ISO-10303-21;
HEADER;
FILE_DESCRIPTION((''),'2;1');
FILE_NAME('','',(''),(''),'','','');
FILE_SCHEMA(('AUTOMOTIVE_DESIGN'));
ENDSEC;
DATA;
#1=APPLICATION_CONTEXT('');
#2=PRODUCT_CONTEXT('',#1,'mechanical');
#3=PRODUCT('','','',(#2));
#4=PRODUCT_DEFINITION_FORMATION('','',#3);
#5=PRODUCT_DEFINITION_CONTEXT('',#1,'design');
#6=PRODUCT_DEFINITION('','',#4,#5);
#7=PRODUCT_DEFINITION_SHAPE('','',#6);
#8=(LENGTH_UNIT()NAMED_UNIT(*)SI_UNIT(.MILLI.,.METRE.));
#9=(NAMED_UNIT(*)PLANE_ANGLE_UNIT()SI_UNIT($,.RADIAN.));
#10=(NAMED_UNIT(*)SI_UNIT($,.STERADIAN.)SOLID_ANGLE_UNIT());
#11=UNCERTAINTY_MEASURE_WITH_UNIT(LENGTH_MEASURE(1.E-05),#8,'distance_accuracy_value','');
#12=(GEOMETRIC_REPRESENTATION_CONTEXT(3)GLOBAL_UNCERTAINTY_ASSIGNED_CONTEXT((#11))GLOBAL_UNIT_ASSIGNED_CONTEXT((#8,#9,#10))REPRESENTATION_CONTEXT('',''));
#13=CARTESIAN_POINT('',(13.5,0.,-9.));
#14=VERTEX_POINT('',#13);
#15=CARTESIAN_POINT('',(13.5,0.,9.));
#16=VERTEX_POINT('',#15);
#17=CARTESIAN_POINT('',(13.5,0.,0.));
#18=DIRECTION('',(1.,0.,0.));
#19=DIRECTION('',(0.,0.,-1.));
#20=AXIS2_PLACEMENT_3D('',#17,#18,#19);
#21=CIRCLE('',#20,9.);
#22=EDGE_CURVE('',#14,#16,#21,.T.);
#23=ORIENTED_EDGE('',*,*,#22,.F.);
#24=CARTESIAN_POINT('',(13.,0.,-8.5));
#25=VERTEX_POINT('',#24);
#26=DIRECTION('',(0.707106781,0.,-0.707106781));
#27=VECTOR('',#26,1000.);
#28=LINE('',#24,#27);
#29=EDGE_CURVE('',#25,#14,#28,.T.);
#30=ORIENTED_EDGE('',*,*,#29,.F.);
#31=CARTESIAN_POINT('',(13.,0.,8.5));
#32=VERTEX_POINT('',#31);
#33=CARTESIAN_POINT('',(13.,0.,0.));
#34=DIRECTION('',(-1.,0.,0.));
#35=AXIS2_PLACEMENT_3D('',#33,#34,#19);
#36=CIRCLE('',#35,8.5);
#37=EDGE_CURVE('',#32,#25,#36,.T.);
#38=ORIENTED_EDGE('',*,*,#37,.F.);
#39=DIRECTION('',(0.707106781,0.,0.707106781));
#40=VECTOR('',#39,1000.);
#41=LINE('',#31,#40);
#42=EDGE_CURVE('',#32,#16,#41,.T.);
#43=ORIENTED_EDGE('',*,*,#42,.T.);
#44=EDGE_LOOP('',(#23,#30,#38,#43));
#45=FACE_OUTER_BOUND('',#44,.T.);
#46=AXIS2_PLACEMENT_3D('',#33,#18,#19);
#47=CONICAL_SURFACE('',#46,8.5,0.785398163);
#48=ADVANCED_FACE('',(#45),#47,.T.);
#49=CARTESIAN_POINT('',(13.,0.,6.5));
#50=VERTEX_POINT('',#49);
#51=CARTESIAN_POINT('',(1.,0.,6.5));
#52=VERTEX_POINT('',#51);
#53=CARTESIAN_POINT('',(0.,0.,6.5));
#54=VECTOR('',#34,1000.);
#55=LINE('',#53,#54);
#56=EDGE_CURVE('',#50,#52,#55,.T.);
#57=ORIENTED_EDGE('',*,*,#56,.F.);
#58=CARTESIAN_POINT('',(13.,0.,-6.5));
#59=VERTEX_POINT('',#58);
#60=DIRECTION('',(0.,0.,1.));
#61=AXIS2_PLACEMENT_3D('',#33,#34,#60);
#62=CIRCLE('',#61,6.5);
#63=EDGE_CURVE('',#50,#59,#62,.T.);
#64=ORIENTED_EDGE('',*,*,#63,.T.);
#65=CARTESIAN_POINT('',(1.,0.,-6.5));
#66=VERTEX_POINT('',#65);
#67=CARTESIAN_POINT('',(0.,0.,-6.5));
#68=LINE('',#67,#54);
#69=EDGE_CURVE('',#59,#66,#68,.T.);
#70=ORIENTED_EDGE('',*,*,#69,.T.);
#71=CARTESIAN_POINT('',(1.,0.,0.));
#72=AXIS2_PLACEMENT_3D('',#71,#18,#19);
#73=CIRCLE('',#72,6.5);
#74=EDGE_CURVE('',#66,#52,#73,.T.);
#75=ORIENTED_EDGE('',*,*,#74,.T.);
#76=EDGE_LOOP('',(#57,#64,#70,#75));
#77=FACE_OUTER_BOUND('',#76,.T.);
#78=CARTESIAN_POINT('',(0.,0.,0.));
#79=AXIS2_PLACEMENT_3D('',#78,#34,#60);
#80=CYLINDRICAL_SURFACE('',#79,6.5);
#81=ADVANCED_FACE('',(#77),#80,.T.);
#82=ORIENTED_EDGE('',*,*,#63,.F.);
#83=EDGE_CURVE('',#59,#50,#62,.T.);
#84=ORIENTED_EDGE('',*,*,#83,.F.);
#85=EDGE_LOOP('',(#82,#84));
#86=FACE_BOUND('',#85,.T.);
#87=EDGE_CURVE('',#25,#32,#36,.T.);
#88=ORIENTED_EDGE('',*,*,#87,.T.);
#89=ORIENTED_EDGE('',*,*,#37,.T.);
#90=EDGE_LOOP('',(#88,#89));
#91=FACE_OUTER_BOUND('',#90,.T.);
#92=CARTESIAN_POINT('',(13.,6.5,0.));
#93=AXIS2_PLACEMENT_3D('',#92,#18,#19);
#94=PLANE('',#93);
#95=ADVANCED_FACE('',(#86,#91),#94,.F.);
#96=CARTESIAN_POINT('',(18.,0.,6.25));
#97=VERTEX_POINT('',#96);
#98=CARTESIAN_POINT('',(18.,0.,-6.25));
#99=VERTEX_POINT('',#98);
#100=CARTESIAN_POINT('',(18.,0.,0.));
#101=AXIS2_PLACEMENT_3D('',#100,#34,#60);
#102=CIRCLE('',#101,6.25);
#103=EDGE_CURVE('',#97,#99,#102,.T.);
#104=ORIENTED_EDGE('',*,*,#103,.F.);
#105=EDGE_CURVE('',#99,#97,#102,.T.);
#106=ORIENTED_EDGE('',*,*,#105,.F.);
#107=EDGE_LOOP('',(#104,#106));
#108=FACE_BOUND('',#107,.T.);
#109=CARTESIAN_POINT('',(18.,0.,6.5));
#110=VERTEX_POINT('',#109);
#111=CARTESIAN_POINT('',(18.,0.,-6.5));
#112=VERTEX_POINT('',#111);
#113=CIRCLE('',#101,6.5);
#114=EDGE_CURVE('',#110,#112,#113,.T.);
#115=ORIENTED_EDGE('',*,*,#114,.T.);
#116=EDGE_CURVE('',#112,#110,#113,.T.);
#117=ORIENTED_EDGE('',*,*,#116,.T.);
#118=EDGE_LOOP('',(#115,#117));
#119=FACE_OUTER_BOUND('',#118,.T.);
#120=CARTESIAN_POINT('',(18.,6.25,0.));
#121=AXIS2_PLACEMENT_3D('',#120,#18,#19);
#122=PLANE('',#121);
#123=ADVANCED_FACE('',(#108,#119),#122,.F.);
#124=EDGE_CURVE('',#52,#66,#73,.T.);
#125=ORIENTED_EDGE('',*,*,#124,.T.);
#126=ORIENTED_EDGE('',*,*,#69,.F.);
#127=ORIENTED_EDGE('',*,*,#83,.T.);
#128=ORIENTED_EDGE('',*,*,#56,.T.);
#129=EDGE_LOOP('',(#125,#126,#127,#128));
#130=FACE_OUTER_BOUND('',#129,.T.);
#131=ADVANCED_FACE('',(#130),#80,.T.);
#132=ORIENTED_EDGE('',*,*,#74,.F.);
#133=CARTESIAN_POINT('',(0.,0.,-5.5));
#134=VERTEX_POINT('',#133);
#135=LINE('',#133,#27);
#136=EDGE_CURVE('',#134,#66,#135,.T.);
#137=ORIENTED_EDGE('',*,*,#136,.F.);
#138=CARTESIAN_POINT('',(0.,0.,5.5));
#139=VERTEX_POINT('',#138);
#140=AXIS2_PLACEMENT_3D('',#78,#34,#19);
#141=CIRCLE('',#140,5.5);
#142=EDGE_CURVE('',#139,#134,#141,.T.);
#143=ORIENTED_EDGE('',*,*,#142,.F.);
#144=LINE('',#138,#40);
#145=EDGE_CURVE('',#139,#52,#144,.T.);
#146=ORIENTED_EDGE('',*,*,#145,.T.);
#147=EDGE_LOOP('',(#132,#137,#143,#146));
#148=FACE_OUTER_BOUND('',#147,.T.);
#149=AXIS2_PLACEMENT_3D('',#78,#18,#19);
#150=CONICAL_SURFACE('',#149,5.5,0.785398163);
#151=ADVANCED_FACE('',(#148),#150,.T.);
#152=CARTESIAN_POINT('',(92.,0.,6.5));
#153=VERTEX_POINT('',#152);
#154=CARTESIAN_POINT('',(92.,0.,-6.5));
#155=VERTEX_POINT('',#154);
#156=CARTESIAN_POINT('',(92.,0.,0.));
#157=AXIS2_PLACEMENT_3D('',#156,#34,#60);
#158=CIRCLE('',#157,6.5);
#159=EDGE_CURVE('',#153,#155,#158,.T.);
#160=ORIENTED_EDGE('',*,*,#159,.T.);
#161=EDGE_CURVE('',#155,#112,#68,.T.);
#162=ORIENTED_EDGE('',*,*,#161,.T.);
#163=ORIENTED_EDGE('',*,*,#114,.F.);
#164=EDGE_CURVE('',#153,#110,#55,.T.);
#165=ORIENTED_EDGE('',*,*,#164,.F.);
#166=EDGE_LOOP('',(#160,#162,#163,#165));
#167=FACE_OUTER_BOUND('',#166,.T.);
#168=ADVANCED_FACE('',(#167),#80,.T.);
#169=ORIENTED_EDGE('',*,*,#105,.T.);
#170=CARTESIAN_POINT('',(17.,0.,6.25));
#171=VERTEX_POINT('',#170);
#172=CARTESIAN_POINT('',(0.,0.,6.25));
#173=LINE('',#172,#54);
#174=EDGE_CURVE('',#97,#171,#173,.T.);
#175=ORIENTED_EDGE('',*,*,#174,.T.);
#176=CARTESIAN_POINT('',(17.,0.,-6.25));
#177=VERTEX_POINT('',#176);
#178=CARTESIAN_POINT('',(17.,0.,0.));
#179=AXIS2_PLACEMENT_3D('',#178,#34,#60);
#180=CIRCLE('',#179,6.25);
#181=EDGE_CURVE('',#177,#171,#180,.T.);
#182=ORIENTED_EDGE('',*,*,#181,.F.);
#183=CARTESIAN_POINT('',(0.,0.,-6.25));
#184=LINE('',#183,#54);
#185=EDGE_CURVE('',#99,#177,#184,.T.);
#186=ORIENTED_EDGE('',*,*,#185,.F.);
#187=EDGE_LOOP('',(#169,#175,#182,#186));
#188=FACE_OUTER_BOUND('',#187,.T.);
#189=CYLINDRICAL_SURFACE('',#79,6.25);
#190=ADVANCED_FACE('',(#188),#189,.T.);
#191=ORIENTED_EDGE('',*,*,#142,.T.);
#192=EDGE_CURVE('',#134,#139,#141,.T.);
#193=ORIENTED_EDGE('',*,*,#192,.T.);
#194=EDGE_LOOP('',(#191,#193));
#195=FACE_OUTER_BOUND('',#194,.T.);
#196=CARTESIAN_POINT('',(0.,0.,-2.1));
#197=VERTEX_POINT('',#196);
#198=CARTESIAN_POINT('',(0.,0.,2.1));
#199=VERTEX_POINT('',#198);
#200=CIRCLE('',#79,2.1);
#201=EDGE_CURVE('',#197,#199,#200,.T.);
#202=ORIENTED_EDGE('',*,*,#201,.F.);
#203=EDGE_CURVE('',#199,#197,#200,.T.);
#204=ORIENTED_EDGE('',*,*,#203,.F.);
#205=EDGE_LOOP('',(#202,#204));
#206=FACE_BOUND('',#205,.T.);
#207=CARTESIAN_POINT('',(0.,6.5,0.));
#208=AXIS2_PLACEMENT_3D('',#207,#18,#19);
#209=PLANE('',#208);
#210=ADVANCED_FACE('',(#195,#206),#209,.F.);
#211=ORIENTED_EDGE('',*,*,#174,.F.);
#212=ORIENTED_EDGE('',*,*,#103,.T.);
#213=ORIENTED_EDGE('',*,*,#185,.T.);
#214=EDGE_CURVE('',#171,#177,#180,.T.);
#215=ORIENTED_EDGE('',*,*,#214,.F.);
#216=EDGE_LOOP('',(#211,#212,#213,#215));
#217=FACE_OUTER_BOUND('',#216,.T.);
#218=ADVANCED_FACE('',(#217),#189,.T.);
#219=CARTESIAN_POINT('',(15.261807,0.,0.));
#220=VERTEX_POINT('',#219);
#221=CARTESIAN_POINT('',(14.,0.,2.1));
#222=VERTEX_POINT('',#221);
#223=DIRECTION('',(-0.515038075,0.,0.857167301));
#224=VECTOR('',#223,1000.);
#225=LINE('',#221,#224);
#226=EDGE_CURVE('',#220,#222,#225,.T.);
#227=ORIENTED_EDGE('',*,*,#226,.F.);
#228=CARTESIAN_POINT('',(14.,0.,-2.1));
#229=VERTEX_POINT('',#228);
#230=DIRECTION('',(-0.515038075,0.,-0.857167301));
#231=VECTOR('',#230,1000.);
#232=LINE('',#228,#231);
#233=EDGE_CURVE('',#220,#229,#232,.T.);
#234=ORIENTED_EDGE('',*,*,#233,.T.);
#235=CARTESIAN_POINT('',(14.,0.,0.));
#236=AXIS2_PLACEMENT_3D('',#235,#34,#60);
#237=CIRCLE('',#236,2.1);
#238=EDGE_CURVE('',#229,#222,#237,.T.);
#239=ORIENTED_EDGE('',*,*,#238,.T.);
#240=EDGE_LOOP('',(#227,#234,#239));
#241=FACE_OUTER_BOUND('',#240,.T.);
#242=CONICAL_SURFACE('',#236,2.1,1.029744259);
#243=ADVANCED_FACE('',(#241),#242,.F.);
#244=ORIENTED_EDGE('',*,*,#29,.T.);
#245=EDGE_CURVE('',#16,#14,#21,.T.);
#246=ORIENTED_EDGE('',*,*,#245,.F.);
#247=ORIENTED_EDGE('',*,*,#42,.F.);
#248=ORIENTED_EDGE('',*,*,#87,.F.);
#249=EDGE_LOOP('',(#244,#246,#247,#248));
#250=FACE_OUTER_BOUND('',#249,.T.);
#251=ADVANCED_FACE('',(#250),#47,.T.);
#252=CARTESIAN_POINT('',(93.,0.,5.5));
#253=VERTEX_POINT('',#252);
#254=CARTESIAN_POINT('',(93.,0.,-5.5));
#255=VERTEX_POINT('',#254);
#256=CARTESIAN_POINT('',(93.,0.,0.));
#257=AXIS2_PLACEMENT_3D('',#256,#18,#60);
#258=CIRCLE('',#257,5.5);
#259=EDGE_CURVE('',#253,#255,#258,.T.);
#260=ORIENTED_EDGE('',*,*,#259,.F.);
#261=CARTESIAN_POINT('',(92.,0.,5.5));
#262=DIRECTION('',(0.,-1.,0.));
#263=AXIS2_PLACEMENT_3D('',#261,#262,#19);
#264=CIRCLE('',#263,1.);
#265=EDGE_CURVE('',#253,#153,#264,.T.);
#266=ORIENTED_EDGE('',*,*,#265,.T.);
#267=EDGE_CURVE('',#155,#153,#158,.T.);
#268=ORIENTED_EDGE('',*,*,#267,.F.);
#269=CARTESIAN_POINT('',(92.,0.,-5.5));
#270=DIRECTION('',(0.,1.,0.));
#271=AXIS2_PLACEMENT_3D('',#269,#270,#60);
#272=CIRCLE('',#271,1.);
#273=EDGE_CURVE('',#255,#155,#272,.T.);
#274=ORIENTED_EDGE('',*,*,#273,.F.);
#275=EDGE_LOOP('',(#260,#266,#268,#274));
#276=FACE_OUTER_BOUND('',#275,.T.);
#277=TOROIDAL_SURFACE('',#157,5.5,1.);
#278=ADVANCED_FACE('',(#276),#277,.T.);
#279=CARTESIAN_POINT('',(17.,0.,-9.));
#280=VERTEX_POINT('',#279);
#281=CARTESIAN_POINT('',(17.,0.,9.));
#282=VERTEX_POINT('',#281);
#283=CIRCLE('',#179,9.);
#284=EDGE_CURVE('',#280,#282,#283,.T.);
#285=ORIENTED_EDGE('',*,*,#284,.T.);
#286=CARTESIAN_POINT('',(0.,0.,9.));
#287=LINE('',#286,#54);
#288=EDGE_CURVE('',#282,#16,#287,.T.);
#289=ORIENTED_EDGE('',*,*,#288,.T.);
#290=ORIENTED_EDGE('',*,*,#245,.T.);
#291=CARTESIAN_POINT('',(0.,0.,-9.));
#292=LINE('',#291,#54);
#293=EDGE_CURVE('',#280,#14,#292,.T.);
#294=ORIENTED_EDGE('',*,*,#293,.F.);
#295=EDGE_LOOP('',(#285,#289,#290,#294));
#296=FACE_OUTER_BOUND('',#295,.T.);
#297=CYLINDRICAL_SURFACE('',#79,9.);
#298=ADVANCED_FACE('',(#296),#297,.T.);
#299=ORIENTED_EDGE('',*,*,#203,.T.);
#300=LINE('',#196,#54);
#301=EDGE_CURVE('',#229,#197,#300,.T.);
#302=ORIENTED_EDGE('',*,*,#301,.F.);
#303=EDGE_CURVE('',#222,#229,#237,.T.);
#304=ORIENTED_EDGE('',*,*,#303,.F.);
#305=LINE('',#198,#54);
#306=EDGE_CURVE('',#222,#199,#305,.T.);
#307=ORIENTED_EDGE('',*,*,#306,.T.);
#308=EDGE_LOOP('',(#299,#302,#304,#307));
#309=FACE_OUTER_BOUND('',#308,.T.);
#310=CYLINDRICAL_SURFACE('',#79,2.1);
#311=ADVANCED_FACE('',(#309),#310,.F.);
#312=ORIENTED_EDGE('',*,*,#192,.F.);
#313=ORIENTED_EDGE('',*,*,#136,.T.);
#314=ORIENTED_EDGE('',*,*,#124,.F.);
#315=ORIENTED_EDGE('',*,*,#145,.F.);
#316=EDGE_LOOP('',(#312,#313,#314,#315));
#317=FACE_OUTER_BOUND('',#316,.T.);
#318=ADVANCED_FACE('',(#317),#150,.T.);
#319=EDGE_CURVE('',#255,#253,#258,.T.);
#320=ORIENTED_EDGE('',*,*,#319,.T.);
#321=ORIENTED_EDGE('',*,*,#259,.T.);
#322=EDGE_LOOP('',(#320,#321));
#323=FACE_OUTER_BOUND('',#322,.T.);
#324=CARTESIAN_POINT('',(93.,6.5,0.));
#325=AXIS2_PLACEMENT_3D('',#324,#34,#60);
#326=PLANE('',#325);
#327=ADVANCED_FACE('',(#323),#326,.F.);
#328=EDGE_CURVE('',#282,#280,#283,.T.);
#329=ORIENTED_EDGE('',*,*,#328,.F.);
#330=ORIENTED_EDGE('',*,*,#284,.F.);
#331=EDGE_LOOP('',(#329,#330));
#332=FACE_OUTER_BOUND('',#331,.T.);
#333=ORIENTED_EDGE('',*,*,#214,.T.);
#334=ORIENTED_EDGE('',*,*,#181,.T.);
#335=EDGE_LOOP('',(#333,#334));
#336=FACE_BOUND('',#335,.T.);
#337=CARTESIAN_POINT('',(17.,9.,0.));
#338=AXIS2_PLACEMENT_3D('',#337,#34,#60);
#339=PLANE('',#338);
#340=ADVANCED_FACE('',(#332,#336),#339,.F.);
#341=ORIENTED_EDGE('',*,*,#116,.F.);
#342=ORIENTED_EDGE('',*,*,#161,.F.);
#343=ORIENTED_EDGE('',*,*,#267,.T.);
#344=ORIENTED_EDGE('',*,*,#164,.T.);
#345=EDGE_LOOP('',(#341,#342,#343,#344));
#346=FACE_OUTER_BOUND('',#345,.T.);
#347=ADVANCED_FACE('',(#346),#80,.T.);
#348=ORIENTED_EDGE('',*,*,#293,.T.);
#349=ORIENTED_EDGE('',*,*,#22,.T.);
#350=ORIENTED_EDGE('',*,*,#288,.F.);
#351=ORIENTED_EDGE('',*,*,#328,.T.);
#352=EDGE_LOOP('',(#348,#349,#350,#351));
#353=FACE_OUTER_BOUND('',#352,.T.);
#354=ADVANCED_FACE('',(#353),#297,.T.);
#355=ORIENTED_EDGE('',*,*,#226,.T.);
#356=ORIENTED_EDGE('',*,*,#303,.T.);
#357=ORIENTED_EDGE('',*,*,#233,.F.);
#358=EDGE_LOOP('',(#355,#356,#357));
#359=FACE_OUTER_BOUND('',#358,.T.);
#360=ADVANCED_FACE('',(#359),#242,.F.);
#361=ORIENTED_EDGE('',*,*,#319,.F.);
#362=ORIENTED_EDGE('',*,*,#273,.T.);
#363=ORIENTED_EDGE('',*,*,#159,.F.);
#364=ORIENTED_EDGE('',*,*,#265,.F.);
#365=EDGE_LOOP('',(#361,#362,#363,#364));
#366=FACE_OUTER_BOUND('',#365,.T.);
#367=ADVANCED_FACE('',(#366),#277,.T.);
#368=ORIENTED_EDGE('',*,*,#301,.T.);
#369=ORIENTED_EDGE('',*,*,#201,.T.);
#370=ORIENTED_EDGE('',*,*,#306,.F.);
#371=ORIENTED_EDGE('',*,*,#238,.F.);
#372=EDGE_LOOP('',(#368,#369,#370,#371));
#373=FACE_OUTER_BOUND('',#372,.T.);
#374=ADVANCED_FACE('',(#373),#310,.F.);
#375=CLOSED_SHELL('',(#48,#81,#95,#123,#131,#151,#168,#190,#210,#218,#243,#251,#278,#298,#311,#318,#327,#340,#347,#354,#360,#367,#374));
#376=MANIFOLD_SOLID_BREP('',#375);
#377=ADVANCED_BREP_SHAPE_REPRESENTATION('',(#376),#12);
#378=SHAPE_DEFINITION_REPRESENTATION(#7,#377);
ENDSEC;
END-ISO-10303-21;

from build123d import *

# Parameters (mm, degrees)
FILLET1_R             = 1
CHAMFER1_SIZE         = 0.5
CHAMFER2_SIZE         = 1
M5_TAPPED_HOLE1_D     = 4.2
M5_TAPPED_HOLE1_DEPTH = 14
M5_TAPPED_HOLE1_TIP   = 1.2618073


with BuildPart() as part:
    # Sketch1 → Revolve1 (revolve)
    with BuildSketch(Plane.XY, mode=Mode.PRIVATE) as revolve1_sk:
        Polygon((13, 6.5), (13, 9), (17, 9), (17, 6.25), (18, 6.25), (18, 6.5), (93, 6.5), (93, 0), (0, 0), (0, 6.5), align=None)
    revolve(revolve1_sk.sketch.rotate(Axis((0, 0, 0), (1, 0, 0)), 90), axis=Axis((0, 0, 0), (1, 0, 0)))

    # Fillet1
    fillet1_edges = [part.edges().sort_by_distance(p)[0] for p in [
        (93, 0, -6.5),
    ]]
    fillet(fillet1_edges, radius=FILLET1_R)

    # Chamfer1
    chamfer1_edges = [part.edges().sort_by_distance(p)[0] for p in [
        (13, 0, -9),
    ]]
    chamfer(chamfer1_edges, length=CHAMFER1_SIZE)

    # Chamfer2
    chamfer2_edges = [part.edges().sort_by_distance(p)[0] for p in [
        (0, 0, -6.5),
    ]]
    chamfer(chamfer2_edges, length=CHAMFER2_SIZE)

    # M5 Tapped Hole1
    with Locations(Plane.ZY):
        with Locations((0, 0)):
            Hole(M5_TAPPED_HOLE1_D / 2, depth=M5_TAPPED_HOLE1_DEPTH)
            with Locations((0, 0, -(M5_TAPPED_HOLE1_DEPTH + M5_TAPPED_HOLE1_TIP / 2))):  # 118° drill point
                Cone(0, M5_TAPPED_HOLE1_D / 2, M5_TAPPED_HOLE1_TIP, mode=Mode.SUBTRACT)


solid = part.part
